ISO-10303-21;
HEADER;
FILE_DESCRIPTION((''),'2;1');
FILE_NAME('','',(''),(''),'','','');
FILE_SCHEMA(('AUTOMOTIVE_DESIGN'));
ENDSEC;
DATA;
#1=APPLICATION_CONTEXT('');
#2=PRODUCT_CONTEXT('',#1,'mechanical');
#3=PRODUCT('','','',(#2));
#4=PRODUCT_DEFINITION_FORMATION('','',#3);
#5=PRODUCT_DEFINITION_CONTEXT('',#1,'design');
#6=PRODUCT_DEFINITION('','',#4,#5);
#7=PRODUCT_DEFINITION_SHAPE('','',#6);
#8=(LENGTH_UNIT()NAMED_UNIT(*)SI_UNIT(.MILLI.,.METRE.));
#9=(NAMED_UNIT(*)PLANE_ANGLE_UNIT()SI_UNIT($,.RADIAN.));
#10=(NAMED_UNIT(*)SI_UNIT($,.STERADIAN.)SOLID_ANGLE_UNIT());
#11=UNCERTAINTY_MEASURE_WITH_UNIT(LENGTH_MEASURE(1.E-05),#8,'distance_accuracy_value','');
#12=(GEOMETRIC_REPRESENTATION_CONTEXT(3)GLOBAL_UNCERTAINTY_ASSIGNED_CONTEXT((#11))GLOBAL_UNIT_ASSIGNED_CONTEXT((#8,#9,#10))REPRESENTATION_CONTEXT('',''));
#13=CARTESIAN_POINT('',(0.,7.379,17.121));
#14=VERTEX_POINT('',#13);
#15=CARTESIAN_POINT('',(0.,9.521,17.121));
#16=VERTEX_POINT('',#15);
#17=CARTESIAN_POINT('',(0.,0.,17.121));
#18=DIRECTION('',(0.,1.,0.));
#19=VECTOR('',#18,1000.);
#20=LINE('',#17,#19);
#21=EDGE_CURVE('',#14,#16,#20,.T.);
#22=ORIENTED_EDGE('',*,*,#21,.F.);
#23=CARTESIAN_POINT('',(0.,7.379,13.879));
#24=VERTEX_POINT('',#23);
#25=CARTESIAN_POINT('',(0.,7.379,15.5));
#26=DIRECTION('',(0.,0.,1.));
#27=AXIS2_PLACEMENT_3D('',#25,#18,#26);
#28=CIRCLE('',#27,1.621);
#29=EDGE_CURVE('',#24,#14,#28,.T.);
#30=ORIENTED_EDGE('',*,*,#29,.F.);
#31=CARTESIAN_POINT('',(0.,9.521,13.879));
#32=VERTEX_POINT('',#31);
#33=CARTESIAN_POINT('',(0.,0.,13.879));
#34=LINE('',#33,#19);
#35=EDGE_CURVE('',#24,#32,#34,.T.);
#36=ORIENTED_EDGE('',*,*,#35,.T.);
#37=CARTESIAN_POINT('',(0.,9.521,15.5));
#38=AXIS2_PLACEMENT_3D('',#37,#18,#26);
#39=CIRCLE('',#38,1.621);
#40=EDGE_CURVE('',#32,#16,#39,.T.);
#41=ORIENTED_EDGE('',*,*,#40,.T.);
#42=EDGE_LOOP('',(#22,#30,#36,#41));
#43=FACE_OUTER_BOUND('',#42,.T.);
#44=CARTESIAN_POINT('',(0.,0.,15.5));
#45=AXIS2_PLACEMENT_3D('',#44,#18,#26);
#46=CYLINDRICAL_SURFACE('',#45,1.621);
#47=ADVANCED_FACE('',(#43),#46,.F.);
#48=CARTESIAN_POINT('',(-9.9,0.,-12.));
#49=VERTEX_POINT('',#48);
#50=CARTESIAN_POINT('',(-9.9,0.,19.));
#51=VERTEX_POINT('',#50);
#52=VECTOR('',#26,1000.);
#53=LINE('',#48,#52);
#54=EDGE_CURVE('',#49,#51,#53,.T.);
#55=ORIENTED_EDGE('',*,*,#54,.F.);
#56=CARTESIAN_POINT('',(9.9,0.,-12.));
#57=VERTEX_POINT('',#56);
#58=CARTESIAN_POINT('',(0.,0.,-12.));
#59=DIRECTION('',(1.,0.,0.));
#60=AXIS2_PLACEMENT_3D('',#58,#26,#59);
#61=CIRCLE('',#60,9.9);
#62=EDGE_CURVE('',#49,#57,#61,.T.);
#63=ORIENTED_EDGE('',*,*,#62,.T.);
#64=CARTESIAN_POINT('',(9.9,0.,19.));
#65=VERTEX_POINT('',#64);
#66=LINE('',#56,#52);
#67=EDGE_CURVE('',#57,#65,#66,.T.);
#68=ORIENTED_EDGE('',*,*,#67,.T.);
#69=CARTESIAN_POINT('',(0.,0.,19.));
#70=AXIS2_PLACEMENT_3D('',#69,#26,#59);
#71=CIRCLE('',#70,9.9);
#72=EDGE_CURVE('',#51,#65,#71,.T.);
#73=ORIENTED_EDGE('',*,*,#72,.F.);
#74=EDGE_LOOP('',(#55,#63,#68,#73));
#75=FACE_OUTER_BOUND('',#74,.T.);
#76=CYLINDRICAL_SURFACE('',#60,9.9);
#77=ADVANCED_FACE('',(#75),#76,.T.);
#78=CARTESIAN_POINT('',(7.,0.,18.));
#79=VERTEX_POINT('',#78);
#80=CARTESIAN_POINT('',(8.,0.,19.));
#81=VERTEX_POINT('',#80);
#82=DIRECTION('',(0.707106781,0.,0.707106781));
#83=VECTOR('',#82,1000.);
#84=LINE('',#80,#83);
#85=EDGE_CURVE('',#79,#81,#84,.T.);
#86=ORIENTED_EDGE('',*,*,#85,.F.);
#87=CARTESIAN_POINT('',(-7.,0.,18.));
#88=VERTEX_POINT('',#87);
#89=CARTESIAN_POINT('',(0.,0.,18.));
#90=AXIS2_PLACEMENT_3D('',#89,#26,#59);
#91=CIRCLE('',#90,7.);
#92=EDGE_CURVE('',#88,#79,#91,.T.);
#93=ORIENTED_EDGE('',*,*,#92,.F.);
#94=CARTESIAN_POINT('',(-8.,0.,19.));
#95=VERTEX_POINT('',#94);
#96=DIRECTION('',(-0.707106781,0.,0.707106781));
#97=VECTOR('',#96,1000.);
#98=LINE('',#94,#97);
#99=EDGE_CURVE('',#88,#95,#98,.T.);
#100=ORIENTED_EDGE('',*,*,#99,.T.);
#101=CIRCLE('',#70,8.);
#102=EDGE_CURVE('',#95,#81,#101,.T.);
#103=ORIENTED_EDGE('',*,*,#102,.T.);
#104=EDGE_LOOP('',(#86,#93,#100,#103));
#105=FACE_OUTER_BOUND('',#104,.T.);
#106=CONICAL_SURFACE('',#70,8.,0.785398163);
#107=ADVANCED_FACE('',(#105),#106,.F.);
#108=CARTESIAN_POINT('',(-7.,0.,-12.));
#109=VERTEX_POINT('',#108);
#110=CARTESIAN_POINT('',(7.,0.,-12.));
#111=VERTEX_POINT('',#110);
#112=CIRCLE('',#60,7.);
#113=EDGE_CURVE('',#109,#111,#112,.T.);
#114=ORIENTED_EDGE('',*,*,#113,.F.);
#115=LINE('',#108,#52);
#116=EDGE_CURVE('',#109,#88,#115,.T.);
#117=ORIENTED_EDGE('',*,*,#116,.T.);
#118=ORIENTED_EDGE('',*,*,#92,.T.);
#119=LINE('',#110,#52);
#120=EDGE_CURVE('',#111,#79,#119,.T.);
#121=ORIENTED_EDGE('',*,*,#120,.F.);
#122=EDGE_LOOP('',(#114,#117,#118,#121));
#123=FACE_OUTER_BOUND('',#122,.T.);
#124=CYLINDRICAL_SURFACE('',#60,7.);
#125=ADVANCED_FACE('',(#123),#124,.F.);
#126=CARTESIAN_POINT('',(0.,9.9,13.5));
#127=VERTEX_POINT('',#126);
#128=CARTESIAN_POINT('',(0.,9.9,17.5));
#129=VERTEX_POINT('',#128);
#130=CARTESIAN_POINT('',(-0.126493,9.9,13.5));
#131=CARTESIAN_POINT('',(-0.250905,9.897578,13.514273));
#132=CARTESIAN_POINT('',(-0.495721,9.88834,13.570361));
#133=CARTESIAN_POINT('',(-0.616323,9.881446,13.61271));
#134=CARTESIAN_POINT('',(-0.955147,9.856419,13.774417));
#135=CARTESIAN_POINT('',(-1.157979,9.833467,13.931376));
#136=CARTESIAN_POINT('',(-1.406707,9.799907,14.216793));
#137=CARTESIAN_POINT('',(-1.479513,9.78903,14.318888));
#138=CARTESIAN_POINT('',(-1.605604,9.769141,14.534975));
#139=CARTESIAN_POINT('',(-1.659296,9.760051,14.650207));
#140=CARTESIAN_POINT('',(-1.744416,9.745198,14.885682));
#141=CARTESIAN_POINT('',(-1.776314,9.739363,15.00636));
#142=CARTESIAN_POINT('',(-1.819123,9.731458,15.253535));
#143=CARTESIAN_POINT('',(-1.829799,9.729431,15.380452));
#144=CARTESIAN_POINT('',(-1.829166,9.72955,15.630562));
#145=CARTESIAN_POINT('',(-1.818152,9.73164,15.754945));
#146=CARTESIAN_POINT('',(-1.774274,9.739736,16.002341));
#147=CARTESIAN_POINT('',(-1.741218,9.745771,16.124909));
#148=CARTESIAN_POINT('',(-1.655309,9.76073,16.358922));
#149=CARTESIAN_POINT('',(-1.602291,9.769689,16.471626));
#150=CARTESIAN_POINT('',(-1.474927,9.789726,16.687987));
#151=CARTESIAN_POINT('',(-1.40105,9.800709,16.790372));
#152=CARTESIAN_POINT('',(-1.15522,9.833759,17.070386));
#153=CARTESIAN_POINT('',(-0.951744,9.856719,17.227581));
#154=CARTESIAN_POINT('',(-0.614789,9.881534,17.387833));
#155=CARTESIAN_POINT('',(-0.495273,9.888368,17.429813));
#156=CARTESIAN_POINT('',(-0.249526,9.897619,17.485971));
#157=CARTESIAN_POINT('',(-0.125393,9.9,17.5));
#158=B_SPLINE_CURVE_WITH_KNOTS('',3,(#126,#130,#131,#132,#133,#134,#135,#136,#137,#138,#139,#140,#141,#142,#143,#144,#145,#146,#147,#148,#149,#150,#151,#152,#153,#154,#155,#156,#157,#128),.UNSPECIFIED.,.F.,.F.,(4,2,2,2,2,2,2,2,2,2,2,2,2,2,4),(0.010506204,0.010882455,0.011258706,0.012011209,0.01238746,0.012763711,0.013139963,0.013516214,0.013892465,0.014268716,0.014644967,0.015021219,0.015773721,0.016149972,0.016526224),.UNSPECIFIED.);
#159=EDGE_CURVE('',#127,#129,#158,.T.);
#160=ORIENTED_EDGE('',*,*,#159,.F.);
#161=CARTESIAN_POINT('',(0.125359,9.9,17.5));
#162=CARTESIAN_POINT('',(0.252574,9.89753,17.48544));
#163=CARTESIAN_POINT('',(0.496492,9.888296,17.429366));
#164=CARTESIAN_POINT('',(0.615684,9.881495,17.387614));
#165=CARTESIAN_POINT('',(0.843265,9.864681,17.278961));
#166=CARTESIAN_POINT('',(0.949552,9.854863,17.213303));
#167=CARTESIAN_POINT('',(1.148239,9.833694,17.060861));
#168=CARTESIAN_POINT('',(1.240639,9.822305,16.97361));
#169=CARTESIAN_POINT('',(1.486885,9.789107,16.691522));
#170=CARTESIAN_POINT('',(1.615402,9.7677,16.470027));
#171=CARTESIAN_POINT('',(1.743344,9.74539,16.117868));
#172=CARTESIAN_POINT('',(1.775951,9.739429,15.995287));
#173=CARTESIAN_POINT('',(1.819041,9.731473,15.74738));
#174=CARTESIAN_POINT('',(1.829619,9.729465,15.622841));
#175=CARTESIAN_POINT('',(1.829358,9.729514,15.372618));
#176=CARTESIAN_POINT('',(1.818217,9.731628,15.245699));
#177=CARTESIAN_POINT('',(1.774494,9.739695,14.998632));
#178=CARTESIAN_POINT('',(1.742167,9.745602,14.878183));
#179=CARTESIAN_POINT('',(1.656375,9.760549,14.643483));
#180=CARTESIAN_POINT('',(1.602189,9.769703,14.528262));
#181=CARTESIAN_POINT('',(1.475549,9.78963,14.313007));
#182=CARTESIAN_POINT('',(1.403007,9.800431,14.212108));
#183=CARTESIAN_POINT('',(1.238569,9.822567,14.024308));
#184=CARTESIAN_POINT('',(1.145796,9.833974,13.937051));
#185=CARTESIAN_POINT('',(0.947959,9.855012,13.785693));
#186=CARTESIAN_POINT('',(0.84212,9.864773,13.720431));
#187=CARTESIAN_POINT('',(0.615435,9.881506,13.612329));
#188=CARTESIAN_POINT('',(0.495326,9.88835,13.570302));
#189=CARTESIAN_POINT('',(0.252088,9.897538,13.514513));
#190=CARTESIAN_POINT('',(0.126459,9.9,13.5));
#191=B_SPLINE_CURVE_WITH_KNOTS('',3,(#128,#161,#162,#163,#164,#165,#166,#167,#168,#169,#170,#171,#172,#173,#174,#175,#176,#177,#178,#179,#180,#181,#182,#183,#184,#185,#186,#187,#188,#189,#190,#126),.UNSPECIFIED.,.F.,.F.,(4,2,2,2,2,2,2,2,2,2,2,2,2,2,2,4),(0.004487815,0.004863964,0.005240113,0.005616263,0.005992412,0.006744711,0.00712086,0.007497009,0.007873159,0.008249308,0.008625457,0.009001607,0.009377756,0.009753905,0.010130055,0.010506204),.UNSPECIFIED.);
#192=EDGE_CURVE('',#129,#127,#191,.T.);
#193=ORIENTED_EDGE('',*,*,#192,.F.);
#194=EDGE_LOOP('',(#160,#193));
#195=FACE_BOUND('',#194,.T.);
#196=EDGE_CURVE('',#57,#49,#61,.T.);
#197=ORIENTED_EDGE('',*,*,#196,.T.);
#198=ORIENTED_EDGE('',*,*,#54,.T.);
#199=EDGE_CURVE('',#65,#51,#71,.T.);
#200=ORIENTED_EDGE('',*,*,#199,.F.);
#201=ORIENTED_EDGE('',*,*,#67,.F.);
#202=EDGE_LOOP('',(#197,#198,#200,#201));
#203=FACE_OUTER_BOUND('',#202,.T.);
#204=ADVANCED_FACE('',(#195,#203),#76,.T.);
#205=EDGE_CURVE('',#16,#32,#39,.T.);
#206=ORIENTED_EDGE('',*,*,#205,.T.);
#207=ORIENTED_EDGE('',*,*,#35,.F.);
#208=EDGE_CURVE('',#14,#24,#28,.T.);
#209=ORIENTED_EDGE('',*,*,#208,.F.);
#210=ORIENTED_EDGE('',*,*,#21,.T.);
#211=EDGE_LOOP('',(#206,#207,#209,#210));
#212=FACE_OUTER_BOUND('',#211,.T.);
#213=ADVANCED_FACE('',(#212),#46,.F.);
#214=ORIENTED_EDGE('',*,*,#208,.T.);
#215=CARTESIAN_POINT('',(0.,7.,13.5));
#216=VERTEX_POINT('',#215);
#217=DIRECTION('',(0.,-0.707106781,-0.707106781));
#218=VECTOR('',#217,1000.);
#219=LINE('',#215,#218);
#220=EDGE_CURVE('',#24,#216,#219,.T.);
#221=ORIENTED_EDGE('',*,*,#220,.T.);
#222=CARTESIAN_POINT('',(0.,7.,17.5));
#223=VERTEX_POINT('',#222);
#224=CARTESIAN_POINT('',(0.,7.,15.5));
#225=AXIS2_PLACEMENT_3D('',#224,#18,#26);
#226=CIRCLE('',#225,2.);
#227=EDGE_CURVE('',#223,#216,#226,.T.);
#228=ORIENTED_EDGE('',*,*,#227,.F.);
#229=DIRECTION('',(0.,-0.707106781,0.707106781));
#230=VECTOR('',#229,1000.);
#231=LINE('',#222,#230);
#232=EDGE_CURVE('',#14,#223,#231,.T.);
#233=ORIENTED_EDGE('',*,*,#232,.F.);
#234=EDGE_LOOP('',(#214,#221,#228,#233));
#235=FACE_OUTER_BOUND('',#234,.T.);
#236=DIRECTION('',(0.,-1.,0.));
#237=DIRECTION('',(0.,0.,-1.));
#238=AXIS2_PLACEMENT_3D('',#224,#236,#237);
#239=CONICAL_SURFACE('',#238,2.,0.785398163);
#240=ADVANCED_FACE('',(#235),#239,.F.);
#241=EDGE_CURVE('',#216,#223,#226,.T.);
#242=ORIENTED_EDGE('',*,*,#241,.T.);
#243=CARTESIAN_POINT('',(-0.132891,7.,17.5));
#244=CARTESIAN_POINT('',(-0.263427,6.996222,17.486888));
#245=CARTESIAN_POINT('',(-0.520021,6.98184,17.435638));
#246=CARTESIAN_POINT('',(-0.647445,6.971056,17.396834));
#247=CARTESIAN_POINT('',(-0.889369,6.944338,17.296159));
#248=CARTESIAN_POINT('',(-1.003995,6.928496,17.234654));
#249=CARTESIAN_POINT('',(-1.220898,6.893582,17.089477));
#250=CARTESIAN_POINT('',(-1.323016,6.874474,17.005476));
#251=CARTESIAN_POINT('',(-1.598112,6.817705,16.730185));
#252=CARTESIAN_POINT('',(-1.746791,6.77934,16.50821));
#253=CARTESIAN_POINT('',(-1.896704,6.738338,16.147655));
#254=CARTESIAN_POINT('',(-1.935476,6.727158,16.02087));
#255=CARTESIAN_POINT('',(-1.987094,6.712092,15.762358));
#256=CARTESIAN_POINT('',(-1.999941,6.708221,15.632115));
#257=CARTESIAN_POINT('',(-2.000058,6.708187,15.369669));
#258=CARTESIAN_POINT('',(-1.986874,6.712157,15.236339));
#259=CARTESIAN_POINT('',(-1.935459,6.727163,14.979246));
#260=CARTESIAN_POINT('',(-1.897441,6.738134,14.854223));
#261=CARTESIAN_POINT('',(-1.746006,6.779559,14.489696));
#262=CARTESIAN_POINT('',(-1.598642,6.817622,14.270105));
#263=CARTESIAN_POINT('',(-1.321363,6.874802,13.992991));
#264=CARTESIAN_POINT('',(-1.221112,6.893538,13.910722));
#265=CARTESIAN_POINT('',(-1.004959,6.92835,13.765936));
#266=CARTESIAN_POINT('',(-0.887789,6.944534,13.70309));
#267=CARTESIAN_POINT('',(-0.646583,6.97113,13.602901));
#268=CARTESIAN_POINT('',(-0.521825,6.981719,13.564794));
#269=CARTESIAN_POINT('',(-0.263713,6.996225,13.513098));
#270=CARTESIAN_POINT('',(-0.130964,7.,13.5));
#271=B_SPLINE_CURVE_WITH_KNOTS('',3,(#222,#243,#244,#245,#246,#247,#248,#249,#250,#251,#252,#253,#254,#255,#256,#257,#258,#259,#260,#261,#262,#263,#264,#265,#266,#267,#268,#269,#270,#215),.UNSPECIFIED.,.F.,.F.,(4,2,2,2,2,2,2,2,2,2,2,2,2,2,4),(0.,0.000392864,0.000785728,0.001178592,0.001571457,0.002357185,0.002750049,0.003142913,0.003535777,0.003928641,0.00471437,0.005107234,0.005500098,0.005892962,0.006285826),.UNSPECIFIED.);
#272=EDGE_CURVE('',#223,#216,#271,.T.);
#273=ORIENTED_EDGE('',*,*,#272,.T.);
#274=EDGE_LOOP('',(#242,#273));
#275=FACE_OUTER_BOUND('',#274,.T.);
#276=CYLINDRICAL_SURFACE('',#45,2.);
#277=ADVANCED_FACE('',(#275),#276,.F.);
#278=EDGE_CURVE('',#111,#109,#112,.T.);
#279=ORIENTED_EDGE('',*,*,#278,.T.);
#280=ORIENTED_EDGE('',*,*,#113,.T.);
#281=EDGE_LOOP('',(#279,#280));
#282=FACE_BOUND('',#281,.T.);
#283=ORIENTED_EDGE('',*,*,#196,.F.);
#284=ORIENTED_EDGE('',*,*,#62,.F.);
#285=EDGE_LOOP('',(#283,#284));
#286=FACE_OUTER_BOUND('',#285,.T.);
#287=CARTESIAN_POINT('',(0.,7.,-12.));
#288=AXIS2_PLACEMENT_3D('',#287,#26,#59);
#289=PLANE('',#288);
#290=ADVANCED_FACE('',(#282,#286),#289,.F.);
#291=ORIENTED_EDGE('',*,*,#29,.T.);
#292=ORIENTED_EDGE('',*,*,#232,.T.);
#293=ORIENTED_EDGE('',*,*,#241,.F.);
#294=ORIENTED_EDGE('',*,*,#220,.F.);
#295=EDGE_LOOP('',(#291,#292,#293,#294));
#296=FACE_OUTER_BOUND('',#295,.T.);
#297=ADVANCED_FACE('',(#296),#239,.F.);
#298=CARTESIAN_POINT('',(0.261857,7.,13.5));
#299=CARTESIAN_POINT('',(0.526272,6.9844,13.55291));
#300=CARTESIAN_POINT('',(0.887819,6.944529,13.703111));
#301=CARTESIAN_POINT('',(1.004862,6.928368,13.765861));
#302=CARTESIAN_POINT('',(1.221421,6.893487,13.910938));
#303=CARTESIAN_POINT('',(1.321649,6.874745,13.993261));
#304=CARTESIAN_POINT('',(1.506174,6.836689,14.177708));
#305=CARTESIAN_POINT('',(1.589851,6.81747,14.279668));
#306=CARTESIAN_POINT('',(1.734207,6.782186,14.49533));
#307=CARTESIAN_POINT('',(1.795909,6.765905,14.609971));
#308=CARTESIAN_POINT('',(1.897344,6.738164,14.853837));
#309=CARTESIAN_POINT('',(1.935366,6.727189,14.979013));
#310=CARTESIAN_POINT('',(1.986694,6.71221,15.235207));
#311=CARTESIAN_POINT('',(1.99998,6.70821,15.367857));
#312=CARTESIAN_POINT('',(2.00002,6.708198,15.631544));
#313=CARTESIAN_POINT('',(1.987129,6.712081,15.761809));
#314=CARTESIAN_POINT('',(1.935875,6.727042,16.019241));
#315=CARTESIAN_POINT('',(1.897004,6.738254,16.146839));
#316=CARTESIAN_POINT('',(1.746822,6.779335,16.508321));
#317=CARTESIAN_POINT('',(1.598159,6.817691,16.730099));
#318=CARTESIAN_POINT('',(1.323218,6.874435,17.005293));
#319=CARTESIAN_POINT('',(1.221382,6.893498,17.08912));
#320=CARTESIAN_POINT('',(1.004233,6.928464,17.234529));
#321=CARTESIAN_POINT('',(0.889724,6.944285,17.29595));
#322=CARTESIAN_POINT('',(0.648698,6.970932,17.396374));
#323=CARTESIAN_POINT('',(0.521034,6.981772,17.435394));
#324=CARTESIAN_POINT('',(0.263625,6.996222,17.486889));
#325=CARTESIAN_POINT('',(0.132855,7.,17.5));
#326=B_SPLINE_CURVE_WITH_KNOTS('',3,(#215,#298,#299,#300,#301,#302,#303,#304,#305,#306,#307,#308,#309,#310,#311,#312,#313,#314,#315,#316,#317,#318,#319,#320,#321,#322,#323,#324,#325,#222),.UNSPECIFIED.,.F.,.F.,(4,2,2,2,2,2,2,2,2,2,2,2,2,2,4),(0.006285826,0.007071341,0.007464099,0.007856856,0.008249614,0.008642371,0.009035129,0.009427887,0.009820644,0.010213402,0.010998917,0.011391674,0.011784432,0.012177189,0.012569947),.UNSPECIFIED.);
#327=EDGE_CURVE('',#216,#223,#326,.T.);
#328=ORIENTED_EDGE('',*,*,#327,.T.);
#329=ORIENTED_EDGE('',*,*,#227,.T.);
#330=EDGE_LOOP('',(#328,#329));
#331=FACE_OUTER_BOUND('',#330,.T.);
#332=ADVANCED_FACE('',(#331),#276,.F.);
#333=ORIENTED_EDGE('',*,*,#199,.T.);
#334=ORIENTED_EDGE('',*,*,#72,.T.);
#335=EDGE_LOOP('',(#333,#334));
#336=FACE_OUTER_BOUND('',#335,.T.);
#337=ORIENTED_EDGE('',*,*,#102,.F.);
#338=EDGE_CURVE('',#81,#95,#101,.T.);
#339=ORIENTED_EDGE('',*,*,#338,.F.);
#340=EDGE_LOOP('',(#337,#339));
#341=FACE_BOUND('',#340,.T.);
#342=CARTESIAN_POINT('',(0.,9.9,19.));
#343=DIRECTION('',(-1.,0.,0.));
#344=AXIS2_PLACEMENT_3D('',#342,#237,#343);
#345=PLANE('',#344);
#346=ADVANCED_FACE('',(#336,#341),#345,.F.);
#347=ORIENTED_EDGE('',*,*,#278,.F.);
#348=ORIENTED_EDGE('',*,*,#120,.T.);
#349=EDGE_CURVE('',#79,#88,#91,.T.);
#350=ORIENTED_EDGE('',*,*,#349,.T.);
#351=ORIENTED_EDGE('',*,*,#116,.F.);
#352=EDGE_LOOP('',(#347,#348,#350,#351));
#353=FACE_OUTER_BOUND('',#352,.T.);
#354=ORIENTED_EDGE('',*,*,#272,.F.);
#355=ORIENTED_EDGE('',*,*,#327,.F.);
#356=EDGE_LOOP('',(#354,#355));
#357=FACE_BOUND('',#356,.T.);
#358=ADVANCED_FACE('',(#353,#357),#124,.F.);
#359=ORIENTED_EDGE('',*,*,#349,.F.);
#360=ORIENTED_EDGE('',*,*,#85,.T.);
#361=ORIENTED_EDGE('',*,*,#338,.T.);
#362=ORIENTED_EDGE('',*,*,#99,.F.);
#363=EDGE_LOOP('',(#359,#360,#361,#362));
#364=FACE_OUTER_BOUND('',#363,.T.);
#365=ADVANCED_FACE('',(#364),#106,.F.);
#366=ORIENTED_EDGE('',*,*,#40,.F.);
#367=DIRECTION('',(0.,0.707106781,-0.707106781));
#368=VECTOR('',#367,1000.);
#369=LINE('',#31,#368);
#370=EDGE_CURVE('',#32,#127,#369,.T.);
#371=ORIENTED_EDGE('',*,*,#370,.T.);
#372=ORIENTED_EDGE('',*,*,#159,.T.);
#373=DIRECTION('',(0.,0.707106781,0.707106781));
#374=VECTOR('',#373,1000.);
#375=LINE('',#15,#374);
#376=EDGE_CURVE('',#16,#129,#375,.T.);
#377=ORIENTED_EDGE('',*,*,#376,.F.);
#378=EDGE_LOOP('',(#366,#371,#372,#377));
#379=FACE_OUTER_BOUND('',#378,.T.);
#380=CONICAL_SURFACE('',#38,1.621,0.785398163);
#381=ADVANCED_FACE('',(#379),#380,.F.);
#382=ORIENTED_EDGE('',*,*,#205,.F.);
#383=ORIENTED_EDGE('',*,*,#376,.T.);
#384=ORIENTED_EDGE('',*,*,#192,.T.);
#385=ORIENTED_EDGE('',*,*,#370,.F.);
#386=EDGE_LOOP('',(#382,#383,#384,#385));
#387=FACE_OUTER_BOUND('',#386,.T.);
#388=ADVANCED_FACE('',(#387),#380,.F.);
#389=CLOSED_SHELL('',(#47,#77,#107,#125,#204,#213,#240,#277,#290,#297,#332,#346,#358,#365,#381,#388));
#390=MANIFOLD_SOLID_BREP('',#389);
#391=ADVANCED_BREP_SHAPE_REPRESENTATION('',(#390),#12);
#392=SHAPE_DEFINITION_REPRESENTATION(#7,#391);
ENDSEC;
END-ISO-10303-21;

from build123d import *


with BuildPart() as part:
    # 草图1 → 旋转1 (revolve)
    with BuildSketch(Plane(origin=(0, 0, 0), x_dir=(0, 0, -1), z_dir=(1, 0, 0)), mode=Mode.PRIVATE) as revolve_1_sk:
        Polygon((-19, 8), (-18, 7), (12, 7), (12, 9.9), (-19, 9.9), align=None)
    revolve(revolve_1_sk.sketch.rotate(Axis((0, 0, -12), (0, 0, 1)), 270), axis=Axis((0, 0, -12), (0, 0, 1)))

    # 草图2 → 切除-旋转1 (revolve, cut)
    with BuildSketch(Plane(origin=(0, 0, 0), x_dir=(0, 0, -1), z_dir=(1, 0, 0)), mode=Mode.PRIVATE) as cut_revolve_1_sk:
        Polygon((-15.5, 9.9), (-13.5, 9.9), (-13.879, 9.521), (-13.879, 7.379), (-13.5, 7), (-13.5, 0), (-15.5, 0), align=None)
    revolve(cut_revolve_1_sk.sketch.rotate(Axis((0, 0, 15.5), (0, 1, 0)), 180), axis=Axis((0, 0, 15.5), (0, 1, 0)), mode=Mode.SUBTRACT)


solid = part.part
